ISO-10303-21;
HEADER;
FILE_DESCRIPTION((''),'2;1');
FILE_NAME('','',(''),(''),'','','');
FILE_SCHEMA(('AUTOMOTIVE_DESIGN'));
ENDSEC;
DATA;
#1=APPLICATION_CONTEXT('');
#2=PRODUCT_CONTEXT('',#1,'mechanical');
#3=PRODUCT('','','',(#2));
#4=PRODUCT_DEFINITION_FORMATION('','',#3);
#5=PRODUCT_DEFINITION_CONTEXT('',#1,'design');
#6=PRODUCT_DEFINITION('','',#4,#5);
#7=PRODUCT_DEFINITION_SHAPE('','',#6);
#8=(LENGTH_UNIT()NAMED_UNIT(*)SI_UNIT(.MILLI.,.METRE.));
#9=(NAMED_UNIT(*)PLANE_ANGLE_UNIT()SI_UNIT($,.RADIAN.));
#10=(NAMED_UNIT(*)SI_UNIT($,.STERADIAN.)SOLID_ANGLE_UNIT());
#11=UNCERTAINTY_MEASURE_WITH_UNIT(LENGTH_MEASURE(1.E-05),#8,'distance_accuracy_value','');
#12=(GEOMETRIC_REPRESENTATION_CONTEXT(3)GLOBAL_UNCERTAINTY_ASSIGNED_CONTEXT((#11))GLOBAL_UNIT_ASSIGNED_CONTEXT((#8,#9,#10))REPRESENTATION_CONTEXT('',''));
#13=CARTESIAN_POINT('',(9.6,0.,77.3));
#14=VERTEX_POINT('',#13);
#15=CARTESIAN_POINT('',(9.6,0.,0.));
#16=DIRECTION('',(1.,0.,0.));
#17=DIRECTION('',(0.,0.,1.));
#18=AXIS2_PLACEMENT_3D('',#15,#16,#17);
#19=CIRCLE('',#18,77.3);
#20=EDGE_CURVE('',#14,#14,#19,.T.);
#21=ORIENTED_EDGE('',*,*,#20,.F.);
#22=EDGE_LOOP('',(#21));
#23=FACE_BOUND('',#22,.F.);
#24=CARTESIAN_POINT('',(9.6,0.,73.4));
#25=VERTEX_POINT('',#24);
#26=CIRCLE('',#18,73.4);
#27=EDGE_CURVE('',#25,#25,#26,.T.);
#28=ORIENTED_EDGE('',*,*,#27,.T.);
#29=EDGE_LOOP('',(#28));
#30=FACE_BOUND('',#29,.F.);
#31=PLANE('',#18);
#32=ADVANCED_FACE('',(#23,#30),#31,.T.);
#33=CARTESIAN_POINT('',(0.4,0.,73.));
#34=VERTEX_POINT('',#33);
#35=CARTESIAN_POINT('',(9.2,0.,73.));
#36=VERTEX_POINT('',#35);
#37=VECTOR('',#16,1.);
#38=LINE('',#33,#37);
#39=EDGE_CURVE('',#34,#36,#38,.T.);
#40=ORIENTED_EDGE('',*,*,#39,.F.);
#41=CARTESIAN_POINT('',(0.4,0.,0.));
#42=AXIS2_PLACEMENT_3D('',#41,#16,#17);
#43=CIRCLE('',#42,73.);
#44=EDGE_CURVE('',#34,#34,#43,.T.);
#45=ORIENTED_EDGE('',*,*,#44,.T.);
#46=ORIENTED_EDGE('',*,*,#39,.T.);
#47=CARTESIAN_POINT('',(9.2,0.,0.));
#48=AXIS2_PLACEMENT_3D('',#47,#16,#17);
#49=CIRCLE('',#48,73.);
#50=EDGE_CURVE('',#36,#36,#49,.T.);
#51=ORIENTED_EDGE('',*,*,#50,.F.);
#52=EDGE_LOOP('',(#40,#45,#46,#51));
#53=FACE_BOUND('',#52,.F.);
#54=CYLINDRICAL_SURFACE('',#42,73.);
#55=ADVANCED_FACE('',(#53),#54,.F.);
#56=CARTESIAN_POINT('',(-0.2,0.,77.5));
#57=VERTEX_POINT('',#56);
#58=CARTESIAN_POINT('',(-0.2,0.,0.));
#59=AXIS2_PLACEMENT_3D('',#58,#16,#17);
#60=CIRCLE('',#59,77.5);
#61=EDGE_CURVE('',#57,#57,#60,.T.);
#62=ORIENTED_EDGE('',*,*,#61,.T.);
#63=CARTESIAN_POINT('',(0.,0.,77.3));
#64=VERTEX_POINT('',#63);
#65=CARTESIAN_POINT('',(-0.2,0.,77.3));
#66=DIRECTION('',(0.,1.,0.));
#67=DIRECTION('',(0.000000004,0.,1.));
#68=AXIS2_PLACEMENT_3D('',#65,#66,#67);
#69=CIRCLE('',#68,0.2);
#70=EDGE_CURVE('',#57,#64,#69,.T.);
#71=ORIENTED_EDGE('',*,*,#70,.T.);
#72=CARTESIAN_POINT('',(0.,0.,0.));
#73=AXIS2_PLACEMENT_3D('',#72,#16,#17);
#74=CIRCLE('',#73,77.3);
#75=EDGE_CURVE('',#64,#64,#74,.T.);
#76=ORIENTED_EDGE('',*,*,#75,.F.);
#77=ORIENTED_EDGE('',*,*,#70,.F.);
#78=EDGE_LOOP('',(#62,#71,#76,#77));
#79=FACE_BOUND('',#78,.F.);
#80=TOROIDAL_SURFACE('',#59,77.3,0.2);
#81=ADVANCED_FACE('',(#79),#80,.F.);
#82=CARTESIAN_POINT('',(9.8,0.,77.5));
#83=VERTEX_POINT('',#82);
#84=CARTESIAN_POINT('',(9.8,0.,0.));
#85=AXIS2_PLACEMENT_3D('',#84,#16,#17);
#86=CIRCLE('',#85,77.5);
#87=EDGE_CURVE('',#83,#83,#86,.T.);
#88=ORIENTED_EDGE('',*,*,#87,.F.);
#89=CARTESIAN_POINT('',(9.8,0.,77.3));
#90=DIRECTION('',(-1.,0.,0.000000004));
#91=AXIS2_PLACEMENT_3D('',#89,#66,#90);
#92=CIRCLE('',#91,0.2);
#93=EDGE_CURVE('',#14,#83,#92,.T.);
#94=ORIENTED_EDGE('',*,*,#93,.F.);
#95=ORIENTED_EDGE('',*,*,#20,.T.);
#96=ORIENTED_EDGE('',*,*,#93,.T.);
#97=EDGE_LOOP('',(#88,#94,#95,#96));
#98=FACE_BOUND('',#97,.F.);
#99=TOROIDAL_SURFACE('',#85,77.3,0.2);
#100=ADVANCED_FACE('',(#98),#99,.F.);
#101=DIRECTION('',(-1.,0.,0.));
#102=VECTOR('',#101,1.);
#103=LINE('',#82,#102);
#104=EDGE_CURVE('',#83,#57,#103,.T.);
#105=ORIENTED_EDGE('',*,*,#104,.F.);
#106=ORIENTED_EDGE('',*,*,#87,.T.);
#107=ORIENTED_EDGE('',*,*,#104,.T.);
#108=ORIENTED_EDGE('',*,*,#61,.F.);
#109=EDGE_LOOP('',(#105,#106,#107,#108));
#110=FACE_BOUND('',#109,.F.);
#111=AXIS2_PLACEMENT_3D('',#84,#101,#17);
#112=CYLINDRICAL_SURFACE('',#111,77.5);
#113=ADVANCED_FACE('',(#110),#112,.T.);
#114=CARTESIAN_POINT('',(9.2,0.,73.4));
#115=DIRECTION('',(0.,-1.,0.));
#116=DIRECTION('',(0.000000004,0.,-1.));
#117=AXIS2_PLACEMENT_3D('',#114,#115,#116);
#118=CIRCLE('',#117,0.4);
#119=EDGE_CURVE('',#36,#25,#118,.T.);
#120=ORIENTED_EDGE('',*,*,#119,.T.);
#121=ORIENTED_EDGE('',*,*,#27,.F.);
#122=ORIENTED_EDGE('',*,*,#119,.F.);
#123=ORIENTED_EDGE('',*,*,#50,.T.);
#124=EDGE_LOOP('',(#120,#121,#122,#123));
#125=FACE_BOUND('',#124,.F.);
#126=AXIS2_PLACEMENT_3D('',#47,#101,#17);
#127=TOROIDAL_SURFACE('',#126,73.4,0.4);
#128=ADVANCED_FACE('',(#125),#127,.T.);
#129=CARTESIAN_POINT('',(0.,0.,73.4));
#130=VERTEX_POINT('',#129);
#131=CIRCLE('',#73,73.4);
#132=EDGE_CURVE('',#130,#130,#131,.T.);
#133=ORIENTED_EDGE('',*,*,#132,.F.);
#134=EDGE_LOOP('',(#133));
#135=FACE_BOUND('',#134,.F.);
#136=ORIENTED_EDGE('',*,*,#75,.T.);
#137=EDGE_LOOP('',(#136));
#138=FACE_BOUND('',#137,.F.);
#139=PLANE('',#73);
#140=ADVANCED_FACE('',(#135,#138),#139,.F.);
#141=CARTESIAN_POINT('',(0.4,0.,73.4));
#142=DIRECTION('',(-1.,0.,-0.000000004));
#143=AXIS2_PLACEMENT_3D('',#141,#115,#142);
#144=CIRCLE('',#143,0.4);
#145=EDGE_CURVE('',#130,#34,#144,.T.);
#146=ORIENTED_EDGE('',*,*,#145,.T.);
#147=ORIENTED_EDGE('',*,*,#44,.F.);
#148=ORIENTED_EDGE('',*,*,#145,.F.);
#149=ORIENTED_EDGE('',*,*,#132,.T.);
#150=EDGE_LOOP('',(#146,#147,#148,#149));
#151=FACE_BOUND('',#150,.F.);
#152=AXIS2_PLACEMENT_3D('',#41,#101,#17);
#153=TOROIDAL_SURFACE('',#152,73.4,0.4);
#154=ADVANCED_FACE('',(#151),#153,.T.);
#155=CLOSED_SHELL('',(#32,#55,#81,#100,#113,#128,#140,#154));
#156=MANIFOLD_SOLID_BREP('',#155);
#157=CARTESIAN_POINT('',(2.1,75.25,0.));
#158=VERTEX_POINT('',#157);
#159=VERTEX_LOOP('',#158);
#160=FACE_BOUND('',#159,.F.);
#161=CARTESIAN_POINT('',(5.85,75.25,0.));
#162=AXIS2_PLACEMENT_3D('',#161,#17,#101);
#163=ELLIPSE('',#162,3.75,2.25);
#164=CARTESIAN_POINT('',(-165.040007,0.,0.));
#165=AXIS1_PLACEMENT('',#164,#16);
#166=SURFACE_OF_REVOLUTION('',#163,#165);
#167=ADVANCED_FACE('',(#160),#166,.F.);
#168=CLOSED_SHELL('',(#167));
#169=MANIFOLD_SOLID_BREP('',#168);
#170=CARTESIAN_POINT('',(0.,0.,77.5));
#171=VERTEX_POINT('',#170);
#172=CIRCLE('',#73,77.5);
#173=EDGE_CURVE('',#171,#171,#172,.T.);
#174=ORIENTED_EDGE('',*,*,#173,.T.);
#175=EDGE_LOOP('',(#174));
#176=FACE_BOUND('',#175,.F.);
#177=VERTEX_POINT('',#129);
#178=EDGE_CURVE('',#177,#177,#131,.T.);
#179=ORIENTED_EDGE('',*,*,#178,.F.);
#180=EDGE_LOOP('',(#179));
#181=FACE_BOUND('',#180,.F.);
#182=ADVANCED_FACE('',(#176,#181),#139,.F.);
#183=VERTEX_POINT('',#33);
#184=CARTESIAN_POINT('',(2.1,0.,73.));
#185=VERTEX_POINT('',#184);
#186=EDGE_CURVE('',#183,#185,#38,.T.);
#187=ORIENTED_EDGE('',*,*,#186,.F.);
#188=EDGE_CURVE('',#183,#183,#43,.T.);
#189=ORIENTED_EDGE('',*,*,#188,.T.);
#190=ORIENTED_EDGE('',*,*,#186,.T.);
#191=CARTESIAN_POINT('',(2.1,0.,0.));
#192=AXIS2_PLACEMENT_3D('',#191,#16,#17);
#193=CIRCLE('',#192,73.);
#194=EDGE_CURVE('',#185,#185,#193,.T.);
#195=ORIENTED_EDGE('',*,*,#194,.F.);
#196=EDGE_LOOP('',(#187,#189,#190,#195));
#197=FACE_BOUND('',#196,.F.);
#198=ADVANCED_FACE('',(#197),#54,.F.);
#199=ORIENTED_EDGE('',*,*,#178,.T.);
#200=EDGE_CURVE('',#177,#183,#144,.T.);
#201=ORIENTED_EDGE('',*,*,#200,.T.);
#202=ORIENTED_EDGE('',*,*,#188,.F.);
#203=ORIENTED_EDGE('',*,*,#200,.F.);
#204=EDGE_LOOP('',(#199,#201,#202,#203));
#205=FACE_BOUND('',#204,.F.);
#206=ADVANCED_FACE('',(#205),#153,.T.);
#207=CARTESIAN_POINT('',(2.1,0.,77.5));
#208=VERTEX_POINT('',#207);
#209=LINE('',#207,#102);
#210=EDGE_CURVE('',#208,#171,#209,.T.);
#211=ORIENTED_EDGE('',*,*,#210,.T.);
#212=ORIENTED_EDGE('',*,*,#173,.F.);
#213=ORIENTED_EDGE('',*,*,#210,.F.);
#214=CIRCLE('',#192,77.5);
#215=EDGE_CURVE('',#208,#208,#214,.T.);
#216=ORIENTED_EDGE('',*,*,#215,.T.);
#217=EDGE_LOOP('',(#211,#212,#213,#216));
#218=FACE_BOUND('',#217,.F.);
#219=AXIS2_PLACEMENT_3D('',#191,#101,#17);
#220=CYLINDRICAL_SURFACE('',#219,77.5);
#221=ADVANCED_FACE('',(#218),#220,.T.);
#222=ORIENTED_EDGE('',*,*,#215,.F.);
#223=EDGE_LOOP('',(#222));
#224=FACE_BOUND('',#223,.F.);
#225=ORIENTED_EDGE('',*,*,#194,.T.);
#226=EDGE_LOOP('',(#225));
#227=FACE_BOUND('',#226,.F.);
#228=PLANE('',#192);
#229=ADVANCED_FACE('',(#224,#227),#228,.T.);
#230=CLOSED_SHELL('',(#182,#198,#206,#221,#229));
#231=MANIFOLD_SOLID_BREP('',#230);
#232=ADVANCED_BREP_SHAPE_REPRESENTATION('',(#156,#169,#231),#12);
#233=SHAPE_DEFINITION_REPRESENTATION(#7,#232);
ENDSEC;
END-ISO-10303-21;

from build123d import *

# Parameters (mm, degrees)
SKETCH_1_RX = 3.75
SKETCH_1_RY = 2.25


with BuildPart() as part:
    # 草图1 → Revolve 688 (revolve)
    with BuildSketch(Plane.XY):
        with Locations(Location((5.85, 75.25), (0, 0, 180))):
            Ellipse(SKETCH_1_RX, SKETCH_1_RY)
    revolve(axis=Axis((-165.040006745, 0, 0), (1, 0, 0)))


with BuildPart() as body_2:
    # 草图1<5> → Revolve 722 (revolve)
    with BuildSketch(Plane.XY, mode=Mode.PRIVATE) as revolve_722_sk:
        with BuildLine():
            Line((0, 77.5), (0, 77.3))
            Line((0, 77.3), (0, 73.4))
            ThreePointArc((0, 73.4), (0.117157288, 73.117157288), (0.4, 73))
            Line((0.4, 73), (2.1, 73))
            Line((2.1, 73), (2.1, 75.25))
            Line((2.1, 75.25), (2.1, 77.5))
            Line((2.1, 77.5), (0, 77.5))
        make_face()
    revolve(revolve_722_sk.sketch.rotate(Axis((-165.040006745, 0, 0), (1, 0, 0)), 90), axis=Axis((-165.040006745, 0, 0), (1, 0, 0)))


with BuildPart() as body_3:
    # 草图1<4> → Revolve 891 (revolve)
    with BuildSketch(Plane.XY, mode=Mode.PRIVATE) as revolve_891_sk:
        with BuildLine():
            Line((0, 77.3), (0, 73.4))
            ThreePointArc((0, 73.4), (0.117157288, 73.117157288), (0.4, 73))
            Line((0.4, 73), (9.2, 73))
            ThreePointArc((9.2, 73), (9.482842712, 73.117157288), (9.6, 73.4))
            Line((9.6, 73.4), (9.6, 77.3))
            ThreePointArc((9.6, 77.3), (9.658578644, 77.441421356), (9.8, 77.5))
            Line((9.8, 77.5), (-0.2, 77.5))
            ThreePointArc((-0.2, 77.5), (-0.058578644, 77.441421356), (0, 77.3))
        make_face()
    revolve(revolve_891_sk.sketch.rotate(Axis((-165.040006745, 0, 0), (1, 0, 0)), 90), axis=Axis((-165.040006745, 0, 0), (1, 0, 0)))


solid = Compound([part.part, body_2.part, body_3.part])
